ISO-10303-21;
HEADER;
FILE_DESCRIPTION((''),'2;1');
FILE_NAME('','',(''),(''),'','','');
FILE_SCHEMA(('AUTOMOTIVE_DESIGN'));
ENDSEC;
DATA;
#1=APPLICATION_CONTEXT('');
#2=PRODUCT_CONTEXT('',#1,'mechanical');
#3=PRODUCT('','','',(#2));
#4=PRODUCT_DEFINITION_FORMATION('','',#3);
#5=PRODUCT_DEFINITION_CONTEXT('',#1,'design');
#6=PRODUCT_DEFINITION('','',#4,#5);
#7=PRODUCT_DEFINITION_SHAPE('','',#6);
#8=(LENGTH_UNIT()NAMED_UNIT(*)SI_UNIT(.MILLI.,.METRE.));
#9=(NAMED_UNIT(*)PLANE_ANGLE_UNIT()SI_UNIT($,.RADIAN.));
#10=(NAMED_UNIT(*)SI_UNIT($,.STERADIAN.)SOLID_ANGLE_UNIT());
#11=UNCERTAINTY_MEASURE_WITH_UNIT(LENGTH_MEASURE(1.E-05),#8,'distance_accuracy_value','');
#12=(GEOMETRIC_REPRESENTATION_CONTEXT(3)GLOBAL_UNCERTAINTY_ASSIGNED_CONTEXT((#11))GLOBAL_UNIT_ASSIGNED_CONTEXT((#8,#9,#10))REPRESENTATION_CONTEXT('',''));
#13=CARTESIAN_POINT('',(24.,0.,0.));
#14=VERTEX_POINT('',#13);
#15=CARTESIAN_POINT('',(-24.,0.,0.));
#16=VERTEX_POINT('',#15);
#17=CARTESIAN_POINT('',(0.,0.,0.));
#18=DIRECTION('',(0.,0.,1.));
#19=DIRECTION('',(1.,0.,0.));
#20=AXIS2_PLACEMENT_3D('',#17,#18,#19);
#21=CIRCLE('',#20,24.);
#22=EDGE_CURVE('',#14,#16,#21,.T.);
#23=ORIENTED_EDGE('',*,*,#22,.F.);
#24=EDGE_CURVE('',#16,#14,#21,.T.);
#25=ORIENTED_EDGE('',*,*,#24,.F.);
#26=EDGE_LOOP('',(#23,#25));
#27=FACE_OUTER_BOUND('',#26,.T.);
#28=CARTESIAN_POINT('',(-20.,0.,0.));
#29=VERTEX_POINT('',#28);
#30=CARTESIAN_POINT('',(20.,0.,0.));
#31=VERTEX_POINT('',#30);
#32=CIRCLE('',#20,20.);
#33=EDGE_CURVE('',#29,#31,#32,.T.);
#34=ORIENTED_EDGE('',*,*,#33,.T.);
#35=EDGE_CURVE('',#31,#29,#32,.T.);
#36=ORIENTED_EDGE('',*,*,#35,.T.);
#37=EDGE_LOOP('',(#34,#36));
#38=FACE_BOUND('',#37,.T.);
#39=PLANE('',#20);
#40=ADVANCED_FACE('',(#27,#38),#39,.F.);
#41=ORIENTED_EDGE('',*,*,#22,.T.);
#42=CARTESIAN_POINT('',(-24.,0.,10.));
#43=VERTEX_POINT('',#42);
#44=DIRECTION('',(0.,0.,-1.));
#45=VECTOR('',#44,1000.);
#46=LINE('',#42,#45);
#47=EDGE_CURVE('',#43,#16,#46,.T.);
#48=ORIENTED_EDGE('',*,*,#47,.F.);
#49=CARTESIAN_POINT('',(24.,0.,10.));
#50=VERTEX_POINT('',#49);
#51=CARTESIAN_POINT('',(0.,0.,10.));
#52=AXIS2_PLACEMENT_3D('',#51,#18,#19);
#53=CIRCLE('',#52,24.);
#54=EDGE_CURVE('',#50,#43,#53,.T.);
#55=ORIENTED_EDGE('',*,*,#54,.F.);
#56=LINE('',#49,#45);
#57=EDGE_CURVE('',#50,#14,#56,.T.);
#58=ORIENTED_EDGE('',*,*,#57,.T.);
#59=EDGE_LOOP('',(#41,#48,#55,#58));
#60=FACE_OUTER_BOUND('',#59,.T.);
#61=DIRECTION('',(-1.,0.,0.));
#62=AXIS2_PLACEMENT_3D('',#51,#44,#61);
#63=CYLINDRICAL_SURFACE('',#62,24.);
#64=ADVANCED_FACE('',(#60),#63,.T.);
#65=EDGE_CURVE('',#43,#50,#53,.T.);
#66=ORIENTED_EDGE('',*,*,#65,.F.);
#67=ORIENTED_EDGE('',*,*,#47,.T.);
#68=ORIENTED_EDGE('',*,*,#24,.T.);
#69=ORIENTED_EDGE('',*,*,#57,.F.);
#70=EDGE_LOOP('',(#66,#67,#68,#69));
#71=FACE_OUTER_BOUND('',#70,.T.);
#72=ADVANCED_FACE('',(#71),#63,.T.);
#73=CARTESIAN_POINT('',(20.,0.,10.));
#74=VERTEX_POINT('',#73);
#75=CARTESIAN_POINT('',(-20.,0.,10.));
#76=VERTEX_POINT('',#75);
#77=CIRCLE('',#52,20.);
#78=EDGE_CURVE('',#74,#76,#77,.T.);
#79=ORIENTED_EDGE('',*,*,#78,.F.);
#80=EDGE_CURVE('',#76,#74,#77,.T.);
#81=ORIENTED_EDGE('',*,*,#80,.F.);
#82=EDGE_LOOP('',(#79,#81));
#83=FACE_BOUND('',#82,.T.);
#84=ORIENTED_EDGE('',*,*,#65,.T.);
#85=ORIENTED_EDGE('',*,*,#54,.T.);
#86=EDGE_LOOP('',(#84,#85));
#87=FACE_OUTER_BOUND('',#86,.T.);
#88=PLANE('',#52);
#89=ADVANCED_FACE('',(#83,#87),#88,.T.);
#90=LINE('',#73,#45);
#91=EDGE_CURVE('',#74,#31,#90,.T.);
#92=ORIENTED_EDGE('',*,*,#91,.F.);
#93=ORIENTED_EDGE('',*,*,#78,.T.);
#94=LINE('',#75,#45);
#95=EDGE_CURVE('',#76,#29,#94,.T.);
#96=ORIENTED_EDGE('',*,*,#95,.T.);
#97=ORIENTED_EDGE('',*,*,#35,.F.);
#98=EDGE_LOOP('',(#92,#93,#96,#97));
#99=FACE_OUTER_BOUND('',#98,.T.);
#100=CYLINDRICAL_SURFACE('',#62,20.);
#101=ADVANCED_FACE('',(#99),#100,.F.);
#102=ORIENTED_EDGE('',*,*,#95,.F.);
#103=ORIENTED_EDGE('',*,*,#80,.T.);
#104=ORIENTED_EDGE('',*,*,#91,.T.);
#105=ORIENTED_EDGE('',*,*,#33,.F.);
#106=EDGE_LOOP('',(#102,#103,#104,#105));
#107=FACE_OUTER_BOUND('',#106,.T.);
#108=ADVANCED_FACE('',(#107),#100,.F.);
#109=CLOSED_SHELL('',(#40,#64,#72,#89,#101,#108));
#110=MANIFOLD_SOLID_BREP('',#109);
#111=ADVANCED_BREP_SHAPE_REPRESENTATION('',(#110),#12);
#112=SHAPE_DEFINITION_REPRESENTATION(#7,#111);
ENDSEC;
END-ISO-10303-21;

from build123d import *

# Parameters (mm, degrees)
SKETCH_2_R      = 24
SKETCH_2_R_2    = 20
EXTRUDE_1_DEPTH = 10


with BuildPart() as part:
    # 草图2 → 凸台-拉伸1 (new body)
    with BuildSketch(Plane.XY):
        Circle(SKETCH_2_R)
        Circle(SKETCH_2_R_2, mode=Mode.SUBTRACT)
    extrude(amount=EXTRUDE_1_DEPTH)


solid = part.part
